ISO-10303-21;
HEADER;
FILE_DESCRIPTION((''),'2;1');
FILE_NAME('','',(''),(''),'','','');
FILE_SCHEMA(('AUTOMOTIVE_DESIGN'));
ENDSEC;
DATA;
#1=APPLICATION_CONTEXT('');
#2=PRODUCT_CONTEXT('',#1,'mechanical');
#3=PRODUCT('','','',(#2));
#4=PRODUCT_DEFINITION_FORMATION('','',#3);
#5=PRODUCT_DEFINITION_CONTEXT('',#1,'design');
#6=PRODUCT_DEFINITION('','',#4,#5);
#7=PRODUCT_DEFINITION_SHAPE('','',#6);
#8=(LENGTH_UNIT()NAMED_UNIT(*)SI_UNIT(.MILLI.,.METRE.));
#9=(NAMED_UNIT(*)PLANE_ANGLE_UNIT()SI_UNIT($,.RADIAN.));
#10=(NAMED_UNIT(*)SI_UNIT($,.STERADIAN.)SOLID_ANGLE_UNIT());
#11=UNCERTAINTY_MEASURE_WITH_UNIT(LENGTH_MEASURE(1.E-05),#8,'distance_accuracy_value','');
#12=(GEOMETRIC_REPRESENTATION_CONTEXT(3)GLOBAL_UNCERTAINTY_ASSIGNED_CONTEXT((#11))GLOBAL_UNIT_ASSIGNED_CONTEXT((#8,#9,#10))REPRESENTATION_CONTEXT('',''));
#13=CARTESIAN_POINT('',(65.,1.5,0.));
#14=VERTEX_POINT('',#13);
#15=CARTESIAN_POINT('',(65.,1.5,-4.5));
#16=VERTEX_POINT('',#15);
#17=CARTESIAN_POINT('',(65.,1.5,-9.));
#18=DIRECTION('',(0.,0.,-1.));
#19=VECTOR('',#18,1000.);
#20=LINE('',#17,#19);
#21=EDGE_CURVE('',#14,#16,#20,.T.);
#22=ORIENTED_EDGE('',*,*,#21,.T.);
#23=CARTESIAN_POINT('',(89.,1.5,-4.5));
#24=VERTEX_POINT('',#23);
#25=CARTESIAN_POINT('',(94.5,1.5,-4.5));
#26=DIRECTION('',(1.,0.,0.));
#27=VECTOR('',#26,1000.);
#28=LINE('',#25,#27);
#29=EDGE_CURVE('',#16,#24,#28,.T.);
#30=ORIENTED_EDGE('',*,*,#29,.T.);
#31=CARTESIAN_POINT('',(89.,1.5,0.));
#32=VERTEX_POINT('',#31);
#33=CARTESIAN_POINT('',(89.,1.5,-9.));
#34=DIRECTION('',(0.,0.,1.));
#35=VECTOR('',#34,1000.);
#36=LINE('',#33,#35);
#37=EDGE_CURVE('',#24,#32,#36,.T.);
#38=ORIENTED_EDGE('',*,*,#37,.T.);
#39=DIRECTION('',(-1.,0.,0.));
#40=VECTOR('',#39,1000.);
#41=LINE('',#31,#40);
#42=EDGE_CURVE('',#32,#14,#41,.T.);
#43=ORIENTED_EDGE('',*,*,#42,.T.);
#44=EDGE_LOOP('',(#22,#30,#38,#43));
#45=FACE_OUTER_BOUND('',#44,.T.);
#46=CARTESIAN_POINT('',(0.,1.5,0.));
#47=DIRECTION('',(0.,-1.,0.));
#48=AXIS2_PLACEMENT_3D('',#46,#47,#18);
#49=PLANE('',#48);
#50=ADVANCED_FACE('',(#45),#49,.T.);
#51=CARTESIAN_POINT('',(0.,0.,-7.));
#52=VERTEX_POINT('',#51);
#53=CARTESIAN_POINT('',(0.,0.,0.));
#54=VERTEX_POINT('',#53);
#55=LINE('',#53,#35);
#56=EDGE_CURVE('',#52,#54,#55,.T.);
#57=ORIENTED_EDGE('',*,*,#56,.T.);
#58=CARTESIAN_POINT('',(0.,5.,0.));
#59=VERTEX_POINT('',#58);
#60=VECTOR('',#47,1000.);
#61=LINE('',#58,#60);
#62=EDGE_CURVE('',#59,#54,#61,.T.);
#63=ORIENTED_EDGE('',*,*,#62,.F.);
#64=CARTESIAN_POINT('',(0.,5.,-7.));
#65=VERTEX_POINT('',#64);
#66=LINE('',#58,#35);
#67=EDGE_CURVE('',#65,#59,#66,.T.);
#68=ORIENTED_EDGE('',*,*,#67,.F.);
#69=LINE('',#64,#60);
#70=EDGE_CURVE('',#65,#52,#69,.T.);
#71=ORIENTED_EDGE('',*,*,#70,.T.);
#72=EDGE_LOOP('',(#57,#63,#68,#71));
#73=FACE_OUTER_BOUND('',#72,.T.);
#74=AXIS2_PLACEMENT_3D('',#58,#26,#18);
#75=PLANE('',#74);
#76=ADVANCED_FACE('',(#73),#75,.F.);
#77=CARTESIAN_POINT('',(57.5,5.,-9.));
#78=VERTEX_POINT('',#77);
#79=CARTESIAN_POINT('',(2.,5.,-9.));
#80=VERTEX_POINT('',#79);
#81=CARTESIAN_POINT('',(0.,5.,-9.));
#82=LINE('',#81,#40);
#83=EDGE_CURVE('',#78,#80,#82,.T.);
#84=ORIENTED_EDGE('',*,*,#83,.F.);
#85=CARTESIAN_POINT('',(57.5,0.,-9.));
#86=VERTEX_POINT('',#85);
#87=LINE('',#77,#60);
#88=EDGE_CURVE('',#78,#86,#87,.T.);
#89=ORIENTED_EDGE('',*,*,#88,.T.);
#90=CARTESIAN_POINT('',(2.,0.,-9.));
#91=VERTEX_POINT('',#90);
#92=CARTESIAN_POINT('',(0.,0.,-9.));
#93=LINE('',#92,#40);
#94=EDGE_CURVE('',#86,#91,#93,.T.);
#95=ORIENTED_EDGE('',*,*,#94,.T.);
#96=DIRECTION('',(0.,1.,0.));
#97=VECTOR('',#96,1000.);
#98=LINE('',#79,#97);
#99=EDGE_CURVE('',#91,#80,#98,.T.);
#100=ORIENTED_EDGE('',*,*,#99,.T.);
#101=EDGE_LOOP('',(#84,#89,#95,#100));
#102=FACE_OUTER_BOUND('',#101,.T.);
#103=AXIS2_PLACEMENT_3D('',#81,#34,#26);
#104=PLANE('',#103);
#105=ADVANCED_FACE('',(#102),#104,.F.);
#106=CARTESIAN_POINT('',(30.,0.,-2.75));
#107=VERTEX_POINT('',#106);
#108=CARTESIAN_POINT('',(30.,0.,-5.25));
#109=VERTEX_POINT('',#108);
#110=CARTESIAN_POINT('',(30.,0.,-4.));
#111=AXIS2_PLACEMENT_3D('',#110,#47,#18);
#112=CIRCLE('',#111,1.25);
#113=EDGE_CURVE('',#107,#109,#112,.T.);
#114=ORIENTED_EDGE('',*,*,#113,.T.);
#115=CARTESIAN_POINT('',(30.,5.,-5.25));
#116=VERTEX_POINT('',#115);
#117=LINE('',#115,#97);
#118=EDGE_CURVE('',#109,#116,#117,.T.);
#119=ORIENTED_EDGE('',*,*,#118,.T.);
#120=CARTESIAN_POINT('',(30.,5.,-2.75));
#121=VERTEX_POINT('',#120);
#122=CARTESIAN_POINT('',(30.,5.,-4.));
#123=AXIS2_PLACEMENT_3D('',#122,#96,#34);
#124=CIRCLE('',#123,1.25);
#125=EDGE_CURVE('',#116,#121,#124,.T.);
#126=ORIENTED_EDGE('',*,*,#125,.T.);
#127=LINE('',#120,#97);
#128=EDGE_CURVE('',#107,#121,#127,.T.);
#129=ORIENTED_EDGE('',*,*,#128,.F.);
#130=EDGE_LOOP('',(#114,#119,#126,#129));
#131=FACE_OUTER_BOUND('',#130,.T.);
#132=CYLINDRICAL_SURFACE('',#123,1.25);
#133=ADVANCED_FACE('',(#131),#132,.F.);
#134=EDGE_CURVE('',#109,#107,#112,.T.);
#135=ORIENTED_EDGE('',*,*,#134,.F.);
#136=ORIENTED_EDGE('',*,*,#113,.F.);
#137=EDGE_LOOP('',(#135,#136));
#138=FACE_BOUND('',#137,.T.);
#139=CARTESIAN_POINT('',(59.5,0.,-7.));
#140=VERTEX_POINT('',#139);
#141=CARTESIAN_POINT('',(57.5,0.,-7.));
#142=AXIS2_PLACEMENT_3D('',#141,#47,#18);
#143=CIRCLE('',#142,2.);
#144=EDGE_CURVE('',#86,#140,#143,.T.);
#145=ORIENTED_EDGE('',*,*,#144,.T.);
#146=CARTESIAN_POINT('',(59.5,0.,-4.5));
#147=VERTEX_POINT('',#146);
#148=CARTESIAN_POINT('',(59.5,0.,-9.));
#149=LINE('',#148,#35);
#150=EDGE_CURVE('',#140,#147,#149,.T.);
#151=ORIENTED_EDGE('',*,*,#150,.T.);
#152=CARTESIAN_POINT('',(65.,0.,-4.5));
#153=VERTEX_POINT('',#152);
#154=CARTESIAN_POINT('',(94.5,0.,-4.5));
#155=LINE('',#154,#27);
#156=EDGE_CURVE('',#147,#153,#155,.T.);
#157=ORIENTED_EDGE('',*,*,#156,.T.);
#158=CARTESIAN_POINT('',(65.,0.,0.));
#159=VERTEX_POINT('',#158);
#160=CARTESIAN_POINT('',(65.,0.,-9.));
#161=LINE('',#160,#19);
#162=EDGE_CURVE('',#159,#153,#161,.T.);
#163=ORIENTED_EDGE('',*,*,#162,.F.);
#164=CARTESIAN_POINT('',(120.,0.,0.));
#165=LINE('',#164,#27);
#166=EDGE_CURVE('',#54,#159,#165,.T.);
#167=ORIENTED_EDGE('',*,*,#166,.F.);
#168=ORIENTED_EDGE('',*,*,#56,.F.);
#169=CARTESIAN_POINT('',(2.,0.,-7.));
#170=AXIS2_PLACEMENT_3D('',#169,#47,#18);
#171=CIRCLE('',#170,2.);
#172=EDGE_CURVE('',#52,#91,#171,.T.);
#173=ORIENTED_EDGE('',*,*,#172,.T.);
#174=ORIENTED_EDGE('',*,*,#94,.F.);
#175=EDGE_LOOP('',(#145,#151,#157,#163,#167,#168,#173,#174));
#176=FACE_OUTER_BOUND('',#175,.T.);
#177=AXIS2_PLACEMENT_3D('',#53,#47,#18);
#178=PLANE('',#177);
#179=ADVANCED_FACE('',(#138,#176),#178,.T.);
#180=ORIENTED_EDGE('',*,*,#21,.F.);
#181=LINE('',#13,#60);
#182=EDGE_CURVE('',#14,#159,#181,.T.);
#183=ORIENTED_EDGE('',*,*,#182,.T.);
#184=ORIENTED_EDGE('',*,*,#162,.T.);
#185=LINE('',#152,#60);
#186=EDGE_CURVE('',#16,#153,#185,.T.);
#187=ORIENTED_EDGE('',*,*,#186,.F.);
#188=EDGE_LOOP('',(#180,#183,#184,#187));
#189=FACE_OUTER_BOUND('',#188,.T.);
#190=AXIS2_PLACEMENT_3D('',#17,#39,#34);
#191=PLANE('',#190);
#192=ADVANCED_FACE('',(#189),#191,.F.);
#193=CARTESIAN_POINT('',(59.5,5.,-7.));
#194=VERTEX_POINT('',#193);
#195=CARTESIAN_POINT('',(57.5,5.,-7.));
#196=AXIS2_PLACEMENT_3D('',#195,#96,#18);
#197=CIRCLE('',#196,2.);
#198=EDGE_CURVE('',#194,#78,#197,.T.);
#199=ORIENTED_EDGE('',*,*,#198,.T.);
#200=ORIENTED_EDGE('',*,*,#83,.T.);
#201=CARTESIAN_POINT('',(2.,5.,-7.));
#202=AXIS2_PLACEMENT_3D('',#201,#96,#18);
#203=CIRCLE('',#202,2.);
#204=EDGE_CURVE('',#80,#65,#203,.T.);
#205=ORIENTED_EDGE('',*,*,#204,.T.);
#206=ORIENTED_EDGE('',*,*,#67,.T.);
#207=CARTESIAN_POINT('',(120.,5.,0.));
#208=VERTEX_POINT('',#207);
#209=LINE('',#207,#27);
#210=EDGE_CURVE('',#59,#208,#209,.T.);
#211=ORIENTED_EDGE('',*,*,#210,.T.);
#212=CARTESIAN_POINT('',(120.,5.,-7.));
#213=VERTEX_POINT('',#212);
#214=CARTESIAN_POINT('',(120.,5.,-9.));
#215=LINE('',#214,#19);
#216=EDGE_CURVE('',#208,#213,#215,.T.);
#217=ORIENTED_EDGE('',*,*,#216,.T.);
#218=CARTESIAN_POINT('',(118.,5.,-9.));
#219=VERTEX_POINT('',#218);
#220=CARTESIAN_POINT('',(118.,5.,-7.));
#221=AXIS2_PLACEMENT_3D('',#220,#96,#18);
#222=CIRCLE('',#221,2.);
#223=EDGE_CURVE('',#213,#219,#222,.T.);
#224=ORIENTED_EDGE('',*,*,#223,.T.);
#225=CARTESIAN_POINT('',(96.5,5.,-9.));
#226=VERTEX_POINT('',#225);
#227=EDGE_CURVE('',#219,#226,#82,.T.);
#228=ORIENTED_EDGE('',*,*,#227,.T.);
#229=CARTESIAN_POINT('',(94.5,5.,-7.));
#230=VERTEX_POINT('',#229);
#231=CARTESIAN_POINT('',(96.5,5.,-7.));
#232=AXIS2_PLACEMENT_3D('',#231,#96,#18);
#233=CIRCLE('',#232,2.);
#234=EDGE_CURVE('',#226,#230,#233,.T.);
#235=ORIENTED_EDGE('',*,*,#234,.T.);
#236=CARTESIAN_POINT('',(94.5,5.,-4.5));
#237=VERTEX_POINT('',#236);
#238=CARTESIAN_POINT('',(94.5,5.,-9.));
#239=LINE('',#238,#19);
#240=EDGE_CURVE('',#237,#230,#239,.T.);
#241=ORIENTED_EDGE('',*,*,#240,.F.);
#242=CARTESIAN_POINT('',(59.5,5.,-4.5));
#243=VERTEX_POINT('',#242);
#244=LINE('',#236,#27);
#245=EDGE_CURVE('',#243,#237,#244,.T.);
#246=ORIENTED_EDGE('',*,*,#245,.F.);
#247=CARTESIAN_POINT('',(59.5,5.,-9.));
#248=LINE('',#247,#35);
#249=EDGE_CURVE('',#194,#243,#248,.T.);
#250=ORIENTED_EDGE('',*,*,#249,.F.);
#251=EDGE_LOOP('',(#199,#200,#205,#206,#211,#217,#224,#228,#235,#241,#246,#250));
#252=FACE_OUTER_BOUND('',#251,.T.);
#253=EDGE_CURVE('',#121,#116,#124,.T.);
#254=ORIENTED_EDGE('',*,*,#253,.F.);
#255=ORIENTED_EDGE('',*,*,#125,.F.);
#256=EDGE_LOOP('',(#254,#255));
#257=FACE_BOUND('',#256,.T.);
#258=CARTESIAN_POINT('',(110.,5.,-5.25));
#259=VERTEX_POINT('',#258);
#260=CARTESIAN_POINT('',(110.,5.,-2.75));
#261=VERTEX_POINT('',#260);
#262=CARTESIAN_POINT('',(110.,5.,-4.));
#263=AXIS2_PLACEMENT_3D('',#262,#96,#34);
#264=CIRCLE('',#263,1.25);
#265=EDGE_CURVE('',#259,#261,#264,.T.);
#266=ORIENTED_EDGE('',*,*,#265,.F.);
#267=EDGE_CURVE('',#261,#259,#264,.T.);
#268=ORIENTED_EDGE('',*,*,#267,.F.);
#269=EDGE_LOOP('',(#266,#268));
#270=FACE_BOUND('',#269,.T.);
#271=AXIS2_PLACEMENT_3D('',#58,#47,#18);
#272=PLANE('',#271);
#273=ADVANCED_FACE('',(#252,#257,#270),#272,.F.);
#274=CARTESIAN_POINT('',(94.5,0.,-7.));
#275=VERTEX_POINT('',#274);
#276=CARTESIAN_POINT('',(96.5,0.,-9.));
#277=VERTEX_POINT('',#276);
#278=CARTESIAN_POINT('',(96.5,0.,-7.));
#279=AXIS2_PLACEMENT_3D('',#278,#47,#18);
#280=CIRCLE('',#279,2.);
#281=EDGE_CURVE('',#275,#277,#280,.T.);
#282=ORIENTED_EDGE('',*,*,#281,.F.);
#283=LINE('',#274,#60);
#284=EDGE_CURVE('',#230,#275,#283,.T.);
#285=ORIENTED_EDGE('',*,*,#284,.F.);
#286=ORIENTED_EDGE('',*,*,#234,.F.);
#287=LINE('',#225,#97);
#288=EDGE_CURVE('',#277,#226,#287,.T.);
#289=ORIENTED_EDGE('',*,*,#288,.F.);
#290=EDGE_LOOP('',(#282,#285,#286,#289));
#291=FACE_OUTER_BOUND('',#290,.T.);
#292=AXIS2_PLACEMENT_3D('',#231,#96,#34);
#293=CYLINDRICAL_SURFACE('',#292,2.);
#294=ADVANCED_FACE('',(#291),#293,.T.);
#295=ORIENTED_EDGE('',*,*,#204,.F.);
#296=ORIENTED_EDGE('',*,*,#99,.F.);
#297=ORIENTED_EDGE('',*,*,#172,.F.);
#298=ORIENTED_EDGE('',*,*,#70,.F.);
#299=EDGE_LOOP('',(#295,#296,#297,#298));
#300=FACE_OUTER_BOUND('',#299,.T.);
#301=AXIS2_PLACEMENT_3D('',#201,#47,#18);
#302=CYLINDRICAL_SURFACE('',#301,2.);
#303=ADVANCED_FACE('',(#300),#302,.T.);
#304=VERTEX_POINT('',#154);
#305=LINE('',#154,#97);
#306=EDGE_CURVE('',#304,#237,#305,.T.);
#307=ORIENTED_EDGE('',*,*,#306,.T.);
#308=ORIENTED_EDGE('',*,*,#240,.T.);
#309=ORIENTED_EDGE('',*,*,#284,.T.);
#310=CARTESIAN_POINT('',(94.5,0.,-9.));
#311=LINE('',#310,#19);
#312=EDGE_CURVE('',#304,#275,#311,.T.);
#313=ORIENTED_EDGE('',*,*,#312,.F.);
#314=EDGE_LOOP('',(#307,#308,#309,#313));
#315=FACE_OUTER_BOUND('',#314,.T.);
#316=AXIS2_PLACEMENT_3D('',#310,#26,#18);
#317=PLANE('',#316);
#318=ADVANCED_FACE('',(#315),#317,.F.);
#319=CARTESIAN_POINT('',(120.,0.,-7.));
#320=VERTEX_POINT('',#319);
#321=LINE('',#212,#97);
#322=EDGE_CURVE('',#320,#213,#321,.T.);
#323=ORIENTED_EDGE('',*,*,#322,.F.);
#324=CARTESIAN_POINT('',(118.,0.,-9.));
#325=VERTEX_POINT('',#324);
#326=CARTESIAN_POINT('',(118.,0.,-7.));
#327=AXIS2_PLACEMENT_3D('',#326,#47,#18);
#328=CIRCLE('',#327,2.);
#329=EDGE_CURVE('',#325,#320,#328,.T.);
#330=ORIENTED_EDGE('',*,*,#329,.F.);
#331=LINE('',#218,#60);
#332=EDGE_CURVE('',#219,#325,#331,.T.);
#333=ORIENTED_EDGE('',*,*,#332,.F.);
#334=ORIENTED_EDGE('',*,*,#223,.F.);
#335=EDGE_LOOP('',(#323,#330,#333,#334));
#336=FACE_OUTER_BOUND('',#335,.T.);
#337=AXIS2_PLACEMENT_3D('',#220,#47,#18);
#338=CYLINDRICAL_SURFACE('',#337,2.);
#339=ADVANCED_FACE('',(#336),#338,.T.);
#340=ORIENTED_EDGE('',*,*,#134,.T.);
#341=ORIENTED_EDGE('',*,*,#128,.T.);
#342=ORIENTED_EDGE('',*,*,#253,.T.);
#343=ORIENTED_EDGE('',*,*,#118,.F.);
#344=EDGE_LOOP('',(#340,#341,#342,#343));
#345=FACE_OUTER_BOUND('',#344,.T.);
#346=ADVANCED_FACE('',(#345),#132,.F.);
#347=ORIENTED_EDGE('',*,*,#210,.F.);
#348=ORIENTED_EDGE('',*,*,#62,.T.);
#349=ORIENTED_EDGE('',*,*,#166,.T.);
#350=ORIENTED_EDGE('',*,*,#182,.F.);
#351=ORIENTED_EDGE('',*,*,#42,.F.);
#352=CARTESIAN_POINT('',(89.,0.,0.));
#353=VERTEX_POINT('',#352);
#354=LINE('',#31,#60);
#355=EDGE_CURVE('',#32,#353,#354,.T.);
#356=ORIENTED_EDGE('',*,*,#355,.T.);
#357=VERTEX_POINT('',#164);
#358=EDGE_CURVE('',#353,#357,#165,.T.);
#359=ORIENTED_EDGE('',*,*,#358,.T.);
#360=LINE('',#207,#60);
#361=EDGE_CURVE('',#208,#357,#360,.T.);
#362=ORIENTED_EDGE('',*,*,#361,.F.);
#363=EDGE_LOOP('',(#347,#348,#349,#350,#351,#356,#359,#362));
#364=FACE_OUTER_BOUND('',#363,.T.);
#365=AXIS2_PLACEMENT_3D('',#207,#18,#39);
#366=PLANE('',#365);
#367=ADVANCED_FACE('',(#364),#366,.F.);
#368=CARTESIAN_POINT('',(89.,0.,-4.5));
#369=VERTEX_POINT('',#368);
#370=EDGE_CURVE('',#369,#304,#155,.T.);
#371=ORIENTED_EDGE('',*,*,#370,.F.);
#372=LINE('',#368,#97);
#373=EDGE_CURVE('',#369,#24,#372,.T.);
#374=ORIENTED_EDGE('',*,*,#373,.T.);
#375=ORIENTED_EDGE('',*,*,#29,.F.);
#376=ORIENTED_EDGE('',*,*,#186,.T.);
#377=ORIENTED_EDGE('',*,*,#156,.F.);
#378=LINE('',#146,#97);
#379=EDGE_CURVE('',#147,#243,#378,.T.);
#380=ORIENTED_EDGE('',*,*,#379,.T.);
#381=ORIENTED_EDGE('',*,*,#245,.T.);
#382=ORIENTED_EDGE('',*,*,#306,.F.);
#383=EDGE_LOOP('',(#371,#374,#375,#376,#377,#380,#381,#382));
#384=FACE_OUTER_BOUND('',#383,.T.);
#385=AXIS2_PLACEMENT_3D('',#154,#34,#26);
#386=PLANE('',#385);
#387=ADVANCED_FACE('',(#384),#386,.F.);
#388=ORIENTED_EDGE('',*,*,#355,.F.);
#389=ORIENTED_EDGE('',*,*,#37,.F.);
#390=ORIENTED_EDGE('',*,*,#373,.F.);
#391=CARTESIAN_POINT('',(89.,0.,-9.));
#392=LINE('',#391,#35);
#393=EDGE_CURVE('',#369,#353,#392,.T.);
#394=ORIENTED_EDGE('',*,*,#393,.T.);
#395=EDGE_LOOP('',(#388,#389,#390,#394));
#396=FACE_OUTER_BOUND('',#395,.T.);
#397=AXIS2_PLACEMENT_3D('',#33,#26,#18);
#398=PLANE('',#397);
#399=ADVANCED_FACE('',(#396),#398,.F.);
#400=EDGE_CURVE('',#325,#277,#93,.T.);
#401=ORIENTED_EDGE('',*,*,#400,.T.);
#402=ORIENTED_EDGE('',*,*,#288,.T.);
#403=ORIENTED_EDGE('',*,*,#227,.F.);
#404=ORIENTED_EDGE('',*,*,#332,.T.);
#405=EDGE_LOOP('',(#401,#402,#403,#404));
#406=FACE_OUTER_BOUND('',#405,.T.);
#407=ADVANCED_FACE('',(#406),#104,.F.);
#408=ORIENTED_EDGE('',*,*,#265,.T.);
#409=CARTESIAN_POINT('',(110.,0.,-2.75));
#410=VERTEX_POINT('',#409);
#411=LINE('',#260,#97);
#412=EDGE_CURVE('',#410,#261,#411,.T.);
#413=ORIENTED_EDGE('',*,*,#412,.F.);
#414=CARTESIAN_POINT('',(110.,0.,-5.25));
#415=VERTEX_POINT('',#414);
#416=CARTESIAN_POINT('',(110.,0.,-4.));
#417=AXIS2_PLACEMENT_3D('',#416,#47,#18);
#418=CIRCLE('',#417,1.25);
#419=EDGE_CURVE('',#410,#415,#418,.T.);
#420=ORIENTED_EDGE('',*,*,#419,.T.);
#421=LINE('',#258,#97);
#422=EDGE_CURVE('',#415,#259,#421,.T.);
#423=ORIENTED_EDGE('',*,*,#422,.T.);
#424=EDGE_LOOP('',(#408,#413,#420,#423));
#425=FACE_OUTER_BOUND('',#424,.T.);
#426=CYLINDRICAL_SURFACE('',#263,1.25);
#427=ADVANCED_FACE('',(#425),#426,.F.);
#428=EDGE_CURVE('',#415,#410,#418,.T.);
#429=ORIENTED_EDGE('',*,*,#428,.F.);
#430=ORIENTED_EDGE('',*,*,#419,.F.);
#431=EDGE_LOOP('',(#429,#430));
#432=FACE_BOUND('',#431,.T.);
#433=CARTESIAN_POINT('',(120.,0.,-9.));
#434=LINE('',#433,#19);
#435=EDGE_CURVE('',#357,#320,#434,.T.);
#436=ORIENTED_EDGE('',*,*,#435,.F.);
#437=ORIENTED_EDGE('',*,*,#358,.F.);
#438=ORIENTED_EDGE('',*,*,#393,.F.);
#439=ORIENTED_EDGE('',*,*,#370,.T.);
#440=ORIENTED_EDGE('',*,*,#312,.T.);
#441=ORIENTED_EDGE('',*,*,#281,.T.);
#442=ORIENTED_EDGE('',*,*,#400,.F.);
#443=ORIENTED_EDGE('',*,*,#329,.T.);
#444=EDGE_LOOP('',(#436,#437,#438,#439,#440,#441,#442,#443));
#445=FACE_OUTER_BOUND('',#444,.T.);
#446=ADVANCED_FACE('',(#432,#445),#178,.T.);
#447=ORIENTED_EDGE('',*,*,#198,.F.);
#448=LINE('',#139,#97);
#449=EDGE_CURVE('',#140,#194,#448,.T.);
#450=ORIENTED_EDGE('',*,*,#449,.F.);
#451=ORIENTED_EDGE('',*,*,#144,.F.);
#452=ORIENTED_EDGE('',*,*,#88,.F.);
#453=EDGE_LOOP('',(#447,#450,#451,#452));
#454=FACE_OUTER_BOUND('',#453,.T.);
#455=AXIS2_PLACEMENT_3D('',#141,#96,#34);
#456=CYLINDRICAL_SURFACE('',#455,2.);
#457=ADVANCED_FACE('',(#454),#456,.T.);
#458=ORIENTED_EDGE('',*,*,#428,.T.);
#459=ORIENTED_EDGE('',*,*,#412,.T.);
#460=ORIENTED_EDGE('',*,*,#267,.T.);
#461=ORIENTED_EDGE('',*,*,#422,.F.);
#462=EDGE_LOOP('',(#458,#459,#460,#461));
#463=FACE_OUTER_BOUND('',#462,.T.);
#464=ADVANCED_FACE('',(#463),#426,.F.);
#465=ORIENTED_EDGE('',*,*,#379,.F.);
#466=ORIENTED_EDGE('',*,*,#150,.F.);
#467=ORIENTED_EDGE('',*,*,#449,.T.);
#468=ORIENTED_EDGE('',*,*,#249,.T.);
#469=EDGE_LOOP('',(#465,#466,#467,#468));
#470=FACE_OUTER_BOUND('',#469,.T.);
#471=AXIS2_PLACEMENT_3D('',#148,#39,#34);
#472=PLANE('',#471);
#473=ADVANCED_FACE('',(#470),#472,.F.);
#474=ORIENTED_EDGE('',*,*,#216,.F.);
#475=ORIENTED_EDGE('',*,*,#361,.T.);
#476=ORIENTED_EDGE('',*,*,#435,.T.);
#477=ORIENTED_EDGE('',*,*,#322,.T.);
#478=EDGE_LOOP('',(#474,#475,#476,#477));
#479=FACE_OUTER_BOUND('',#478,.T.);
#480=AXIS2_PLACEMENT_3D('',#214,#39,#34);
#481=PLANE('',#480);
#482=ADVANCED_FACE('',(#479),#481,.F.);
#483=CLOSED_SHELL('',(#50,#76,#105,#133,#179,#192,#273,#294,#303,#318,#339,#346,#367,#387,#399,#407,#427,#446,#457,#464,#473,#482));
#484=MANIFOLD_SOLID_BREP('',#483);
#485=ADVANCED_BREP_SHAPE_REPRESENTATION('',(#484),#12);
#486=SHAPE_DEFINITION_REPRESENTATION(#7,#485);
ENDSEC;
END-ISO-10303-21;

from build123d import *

# Parameters (mm, degrees)
SKETCH1_W             = 120
SKETCH1_H             = 9
BOSS_EXTRUDE1_DEPTH   = 5
M3_TAPPED_HOLE1_D     = 2.5
M3_TAPPED_HOLE1_DEPTH = 8.5
FILLET1_R             = 2
SKETCH4_W             = 35
SKETCH4_H             = 4.5
CUT_EXTRUDE1_DEPTH    = 121.440856855
FILLET2_R             = 2
SKETCH5_W             = 24
SKETCH5_H             = 9
CUT_EXTRUDE2_DEPTH    = 1.5


with BuildPart() as part:
    # Sketch1 → Boss-Extrude1 (new body)
    with BuildSketch(Plane(origin=(0, 0, 0), x_dir=(1, 0, 0), z_dir=(0, 1, 0))):
        with Locations((60, 4.5)):
            Rectangle(SKETCH1_W, SKETCH1_H)
    extrude(amount=BOSS_EXTRUDE1_DEPTH)

    # M3 Tapped Hole1
    with Locations(Plane(origin=(0, 5, 0), x_dir=(-1, 0, 0), z_dir=(0, 1, 0))):
        with Locations((-30, -4), (-110, -4)):
            Hole(M3_TAPPED_HOLE1_D / 2, depth=M3_TAPPED_HOLE1_DEPTH)

    # Fillet1
    fillet1_edges = [part.edges().sort_by_distance(p)[0] for p in [
        (0, 2.5, -9),
        (120, 2.5, -9),
    ]]
    fillet(fillet1_edges, radius=FILLET1_R)

    # Sketch4 → Cut-Extrude1 (cut, through all)
    with BuildSketch(Plane(origin=(0, 5, 0), x_dir=(-1, 0, 0), z_dir=(0, 1, 0))):
        with Locations((-77, -6.75)):
            Rectangle(SKETCH4_W, SKETCH4_H)
    extrude(amount=-CUT_EXTRUDE1_DEPTH, mode=Mode.SUBTRACT)

    # Fillet2
    fillet2_edges = [part.edges().sort_by_distance(p)[0] for p in [
        (94.5, 2.5, -9),
        (59.5, 2.5, -9),
    ]]
    fillet(fillet2_edges, radius=FILLET2_R)

    # Sketch5 → Cut-Extrude2 (cut)
    with BuildSketch(Plane.XZ):
        with Locations((77, -4.5)):
            Rectangle(SKETCH5_W, SKETCH5_H)
    extrude(amount=-CUT_EXTRUDE2_DEPTH, mode=Mode.SUBTRACT)


solid = part.part
